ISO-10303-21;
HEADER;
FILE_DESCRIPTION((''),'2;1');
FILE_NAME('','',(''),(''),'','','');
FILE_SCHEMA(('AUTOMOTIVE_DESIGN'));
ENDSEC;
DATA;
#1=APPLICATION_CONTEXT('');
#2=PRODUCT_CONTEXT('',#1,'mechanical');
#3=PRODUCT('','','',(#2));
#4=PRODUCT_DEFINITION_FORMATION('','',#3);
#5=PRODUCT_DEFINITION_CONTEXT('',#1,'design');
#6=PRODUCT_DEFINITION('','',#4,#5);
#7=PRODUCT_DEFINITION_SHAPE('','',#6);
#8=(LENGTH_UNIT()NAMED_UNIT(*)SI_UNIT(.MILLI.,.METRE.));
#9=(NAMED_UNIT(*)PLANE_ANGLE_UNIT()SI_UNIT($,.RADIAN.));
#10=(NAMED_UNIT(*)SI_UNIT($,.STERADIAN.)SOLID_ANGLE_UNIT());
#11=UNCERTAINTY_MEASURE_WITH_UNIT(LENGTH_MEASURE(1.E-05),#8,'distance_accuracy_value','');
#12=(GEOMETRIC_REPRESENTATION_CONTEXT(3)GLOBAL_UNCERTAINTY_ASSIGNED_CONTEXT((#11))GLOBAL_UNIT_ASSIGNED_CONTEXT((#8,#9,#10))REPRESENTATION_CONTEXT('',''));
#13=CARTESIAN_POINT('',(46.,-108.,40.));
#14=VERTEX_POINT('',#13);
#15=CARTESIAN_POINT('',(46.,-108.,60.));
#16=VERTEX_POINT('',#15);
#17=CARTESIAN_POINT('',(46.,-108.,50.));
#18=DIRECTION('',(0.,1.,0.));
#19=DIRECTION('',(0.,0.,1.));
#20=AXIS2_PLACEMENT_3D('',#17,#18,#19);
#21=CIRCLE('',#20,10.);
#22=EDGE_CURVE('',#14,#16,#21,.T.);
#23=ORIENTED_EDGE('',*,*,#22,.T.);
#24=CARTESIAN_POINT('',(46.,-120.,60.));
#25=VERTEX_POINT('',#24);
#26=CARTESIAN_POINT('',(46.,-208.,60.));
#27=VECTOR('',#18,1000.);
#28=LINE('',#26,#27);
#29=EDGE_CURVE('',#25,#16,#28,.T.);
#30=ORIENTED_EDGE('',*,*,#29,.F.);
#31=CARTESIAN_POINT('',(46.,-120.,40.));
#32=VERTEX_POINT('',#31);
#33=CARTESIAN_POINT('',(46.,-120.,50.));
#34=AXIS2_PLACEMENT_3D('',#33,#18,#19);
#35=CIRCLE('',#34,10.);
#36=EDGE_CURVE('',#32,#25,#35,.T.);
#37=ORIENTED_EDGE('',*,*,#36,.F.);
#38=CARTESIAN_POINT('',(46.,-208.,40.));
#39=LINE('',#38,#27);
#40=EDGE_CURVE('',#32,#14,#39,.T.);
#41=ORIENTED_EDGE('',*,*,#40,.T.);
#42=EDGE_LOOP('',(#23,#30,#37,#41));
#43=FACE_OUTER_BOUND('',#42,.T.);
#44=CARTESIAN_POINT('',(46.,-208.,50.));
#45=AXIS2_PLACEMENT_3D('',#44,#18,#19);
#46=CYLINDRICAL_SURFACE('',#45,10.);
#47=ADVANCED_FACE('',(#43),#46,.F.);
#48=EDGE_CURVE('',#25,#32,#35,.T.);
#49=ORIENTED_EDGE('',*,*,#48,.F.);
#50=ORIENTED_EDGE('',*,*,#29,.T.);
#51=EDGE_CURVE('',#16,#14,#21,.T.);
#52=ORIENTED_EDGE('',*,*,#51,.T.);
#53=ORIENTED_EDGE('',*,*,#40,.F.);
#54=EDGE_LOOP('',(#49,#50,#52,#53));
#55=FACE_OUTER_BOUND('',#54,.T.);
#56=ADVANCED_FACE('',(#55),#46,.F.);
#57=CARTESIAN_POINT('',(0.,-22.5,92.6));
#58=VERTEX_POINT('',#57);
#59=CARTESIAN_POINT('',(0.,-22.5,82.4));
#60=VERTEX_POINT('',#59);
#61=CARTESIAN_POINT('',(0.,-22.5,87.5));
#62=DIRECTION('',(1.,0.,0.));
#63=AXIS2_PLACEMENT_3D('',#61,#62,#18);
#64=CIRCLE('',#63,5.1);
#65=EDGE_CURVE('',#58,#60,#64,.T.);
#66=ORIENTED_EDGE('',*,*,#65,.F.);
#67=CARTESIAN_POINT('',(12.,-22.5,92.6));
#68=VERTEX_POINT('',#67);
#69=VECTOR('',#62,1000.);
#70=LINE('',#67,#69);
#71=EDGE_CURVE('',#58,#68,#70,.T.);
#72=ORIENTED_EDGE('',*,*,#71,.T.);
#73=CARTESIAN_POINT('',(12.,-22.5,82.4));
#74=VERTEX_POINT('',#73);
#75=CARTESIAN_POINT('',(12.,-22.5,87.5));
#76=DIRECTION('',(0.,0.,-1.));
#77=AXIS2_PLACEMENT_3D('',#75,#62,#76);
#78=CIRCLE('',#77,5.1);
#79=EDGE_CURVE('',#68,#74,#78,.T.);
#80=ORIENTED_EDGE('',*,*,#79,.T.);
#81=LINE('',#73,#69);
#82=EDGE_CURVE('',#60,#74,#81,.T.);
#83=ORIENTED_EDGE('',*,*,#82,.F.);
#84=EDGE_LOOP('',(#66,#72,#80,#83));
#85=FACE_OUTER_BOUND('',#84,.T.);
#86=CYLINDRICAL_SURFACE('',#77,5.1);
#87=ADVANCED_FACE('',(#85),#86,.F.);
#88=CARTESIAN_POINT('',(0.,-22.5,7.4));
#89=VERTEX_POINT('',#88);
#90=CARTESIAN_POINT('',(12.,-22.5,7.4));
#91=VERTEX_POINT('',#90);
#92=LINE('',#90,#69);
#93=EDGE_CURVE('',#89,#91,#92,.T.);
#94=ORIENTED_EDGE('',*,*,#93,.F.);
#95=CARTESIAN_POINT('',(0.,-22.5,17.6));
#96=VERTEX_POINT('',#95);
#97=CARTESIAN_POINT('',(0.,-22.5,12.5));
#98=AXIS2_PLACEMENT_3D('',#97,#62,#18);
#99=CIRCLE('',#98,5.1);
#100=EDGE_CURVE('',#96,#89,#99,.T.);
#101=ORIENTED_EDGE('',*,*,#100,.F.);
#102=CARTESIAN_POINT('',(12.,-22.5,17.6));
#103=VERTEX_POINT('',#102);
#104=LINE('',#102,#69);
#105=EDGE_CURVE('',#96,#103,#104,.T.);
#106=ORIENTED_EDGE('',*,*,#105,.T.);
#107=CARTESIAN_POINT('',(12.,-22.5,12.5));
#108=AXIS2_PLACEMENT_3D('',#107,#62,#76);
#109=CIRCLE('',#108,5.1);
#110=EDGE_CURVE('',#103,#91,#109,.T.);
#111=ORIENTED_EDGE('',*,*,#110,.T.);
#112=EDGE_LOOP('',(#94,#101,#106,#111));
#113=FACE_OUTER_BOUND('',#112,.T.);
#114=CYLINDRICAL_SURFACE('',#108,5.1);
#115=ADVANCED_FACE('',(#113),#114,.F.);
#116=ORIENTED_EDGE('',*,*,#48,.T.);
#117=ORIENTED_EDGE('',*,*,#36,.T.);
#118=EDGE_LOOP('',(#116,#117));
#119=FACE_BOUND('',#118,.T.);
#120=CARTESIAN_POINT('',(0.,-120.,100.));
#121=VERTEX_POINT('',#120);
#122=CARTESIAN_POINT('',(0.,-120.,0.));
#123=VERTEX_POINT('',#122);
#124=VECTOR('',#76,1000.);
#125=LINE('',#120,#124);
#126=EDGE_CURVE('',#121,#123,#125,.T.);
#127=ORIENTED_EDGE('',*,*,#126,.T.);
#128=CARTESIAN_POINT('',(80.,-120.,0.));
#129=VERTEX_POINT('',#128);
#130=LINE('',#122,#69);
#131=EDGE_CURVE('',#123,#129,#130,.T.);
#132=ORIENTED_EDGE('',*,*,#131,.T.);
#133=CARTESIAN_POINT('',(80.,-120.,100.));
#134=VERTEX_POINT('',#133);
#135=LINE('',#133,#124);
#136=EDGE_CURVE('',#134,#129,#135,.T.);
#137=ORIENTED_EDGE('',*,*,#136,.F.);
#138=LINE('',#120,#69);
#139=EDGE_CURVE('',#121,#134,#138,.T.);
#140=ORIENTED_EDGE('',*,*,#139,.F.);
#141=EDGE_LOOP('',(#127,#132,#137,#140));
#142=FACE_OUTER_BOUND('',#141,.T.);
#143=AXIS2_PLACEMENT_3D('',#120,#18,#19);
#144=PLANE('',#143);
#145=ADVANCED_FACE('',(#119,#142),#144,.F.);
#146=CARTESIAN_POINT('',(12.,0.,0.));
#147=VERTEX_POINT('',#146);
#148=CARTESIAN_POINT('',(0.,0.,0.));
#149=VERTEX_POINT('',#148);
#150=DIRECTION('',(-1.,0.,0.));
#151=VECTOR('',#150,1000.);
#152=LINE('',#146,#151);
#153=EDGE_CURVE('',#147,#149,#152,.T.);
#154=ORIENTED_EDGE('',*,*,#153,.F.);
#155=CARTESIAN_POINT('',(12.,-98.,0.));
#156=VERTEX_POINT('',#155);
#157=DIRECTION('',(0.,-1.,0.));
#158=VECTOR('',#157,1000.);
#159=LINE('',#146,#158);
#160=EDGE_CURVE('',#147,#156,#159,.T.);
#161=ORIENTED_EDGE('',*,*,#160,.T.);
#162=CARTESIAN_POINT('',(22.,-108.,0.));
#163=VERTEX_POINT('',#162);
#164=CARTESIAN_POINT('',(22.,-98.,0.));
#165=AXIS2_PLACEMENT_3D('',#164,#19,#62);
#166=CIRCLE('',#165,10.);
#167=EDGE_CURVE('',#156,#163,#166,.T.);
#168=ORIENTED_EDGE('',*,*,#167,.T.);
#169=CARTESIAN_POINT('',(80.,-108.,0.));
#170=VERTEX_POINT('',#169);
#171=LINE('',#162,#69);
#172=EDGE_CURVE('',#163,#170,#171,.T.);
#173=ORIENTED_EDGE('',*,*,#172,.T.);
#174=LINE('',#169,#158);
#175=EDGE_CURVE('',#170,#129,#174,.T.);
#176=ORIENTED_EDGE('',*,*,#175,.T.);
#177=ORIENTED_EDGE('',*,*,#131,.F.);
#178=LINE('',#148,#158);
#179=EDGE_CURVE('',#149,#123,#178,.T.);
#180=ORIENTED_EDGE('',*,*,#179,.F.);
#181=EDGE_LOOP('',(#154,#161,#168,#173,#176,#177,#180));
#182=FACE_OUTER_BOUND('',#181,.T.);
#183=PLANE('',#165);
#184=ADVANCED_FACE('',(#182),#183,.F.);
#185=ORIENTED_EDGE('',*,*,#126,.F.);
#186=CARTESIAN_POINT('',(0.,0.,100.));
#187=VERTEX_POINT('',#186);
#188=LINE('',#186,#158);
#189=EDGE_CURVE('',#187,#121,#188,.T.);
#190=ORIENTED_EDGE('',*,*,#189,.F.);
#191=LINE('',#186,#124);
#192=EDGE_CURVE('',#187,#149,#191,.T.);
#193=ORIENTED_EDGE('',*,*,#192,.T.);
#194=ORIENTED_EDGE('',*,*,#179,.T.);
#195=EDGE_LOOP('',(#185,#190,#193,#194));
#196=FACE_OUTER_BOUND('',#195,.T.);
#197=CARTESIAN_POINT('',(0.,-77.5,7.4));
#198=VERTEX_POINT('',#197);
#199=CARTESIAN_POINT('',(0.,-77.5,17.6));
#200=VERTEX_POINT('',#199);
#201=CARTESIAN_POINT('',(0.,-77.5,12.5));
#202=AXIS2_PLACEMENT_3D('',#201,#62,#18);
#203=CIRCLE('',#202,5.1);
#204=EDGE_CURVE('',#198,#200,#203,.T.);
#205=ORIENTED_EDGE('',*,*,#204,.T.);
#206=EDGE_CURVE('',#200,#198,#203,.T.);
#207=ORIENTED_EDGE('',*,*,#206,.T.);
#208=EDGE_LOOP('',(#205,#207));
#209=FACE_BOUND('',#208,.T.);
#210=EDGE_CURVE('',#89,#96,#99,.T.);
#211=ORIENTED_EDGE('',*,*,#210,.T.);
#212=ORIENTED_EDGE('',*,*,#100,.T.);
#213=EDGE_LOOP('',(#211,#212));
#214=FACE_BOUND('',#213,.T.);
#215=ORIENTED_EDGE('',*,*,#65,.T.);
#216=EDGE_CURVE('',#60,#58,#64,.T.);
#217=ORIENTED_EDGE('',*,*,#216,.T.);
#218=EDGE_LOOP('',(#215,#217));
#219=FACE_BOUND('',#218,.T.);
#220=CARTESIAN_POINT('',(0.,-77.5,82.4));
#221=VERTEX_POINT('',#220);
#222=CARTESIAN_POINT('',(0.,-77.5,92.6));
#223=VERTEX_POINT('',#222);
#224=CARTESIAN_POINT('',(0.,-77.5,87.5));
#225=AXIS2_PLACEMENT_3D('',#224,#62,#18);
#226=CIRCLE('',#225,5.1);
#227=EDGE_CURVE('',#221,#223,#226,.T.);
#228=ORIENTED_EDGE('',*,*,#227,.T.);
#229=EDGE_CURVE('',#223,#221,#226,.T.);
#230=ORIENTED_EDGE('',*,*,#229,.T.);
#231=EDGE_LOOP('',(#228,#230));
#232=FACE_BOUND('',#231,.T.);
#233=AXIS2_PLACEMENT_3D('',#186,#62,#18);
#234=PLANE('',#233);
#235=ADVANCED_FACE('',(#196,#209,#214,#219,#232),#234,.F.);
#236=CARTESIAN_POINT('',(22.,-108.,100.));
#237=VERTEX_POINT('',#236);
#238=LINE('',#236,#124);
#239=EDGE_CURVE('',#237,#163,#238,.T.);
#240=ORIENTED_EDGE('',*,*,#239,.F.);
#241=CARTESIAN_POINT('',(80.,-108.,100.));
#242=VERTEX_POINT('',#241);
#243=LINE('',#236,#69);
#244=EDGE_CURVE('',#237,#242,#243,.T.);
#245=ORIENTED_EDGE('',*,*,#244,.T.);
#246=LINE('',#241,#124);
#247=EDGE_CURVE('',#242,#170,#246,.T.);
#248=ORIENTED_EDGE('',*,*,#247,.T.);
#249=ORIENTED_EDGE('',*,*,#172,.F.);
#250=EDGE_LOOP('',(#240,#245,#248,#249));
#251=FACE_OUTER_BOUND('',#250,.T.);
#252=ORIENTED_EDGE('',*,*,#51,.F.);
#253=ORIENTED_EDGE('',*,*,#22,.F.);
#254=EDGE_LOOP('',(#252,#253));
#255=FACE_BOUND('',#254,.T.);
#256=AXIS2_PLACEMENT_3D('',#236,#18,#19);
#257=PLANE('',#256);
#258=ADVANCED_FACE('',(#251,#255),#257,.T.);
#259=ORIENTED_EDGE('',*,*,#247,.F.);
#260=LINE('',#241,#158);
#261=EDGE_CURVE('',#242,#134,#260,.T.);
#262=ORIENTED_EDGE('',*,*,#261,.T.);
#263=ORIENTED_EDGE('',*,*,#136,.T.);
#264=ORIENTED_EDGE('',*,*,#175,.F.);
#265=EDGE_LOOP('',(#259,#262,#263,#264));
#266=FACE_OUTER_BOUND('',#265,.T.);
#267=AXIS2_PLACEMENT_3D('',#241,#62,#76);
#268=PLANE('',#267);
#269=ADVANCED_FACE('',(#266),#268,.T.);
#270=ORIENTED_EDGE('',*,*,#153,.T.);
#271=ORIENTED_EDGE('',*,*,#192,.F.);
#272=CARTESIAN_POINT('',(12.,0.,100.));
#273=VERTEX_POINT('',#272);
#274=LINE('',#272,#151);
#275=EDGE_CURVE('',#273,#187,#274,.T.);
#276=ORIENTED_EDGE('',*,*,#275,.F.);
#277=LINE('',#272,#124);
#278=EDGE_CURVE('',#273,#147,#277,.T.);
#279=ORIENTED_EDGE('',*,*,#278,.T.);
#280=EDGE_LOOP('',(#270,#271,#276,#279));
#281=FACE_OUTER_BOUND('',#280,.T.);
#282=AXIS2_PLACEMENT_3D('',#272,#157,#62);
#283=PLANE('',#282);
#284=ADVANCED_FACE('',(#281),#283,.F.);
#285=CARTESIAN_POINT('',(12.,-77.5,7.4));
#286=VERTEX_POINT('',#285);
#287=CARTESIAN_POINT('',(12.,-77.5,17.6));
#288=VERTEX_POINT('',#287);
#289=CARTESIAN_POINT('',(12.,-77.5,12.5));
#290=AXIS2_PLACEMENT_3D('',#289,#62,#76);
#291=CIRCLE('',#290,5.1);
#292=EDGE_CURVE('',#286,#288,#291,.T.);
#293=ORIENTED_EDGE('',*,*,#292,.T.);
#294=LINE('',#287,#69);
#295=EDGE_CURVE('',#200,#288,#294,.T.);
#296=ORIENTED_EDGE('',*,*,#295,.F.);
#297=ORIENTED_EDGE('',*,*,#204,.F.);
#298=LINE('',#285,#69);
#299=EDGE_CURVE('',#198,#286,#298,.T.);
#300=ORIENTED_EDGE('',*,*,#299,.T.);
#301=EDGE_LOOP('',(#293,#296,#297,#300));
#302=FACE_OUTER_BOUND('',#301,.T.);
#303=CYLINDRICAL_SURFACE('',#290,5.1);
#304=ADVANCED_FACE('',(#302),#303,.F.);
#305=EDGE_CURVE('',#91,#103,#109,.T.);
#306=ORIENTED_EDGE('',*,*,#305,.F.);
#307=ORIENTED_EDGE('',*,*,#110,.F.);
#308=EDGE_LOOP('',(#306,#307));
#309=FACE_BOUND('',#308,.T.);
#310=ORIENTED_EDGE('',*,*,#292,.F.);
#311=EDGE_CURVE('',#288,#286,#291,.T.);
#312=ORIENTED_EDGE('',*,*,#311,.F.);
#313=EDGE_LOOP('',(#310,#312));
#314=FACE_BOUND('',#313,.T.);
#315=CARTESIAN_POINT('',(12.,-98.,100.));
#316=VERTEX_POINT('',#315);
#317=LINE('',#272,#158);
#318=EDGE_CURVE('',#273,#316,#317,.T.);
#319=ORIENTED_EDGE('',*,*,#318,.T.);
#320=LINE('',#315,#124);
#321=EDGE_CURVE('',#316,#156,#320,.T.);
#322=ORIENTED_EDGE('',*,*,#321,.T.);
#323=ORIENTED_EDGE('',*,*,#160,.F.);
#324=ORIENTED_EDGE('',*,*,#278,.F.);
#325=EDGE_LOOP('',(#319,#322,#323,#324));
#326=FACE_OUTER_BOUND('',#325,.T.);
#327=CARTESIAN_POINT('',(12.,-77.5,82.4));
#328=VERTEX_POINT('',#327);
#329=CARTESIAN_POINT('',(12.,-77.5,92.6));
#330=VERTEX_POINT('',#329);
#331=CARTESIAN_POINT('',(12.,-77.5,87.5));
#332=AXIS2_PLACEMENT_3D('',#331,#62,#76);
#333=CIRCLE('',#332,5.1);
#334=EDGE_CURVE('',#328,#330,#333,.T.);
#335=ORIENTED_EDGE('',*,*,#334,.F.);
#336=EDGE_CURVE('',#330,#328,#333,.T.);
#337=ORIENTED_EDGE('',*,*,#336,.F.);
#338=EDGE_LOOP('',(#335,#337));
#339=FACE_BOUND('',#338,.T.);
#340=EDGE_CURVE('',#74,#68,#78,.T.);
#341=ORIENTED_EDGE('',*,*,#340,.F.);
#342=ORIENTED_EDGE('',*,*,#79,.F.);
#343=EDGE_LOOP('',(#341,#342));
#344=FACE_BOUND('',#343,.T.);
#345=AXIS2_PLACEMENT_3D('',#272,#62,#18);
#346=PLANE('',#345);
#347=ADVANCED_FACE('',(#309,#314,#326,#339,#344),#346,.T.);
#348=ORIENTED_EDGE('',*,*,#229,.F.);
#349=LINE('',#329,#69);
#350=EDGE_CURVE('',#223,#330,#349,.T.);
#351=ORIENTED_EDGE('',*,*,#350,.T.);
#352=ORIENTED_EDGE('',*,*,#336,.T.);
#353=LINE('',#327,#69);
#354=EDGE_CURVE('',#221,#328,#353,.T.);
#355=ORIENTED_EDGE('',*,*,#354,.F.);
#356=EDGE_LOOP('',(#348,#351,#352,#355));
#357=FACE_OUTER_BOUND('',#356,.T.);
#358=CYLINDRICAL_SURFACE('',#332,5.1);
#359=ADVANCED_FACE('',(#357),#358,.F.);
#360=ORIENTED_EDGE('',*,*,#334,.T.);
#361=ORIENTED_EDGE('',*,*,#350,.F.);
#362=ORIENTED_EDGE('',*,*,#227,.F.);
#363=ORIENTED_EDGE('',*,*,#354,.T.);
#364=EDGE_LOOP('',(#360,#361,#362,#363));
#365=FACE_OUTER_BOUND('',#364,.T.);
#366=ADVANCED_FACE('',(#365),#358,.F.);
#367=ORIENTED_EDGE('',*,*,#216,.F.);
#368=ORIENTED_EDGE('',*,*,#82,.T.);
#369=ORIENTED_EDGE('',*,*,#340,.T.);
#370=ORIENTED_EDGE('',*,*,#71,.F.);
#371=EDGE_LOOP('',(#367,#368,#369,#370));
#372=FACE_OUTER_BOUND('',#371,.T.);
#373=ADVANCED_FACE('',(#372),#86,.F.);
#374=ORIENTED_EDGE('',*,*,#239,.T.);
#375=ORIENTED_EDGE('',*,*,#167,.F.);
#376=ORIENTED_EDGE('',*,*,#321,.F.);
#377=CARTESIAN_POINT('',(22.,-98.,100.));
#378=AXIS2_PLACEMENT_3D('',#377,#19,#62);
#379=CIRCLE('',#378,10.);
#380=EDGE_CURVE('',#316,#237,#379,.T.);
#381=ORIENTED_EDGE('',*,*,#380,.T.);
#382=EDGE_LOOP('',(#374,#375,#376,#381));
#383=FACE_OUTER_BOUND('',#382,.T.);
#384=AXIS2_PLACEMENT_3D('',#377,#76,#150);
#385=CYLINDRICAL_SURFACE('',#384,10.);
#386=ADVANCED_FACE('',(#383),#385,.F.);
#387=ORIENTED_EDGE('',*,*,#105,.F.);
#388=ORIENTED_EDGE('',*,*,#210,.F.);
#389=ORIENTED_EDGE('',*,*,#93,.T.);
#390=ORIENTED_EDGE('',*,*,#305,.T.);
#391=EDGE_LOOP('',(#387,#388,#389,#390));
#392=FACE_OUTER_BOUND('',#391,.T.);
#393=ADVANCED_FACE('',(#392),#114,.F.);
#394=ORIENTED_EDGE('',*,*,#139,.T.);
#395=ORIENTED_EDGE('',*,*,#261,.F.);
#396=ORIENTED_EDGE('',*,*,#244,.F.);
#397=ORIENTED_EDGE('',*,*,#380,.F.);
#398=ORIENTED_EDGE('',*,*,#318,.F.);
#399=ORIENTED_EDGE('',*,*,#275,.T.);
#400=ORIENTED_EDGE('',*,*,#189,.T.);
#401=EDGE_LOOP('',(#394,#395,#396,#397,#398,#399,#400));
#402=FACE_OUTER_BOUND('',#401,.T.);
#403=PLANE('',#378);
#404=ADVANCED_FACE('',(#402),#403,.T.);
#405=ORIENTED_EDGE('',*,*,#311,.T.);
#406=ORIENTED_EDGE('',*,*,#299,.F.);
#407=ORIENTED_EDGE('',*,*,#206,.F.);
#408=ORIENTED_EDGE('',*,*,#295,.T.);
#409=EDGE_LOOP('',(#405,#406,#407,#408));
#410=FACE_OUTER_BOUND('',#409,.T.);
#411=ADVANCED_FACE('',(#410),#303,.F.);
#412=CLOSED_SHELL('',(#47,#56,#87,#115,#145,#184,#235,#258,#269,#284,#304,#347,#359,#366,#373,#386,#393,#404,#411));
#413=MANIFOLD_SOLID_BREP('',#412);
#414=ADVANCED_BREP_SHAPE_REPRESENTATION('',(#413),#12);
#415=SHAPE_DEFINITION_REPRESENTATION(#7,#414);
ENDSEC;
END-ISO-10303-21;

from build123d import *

# Parameters (mm, degrees)
BOSS_EXTRUDE1_DEPTH    = 100
M12_TAPPED_HOLE1_D     = 10.2
M12_TAPPED_HOLE1_DEPTH = 29.25
M12_TAPPED_HOLE1_TIP   = 3.064389157
SKETCH5_R              = 10
CUT_EXTRUDE1_DEPTH     = 100


with BuildPart() as part:
    # Sketch1 → Boss-Extrude1 (new body)
    with BuildSketch(Plane.XY):
        with BuildLine():
            Line((0, 0), (0, -120))
            Line((0, -120), (80, -120))
            Line((80, -120), (80, -108))
            Line((80, -108), (22, -108))
            ThreePointArc((22, -108), (14.928932188, -105.071067812), (12, -98))
            Line((12, -98), (12, 0))
            Line((12, 0), (0, 0))
        make_face()
    extrude(amount=BOSS_EXTRUDE1_DEPTH)

    # M12 Tapped Hole1
    with Locations(Plane(origin=(12, 0, 0), x_dir=(0, 0, -1), z_dir=(1, 0, 0))):
        with Locations((-87.5, -22.5), (-12.5, -22.5), (-12.5, -77.5), (-87.5, -77.5)):
            Hole(M12_TAPPED_HOLE1_D / 2, depth=M12_TAPPED_HOLE1_DEPTH)
            with Locations((0, 0, -(M12_TAPPED_HOLE1_DEPTH + M12_TAPPED_HOLE1_TIP / 2))):  # 118° drill point
                Cone(0, M12_TAPPED_HOLE1_D / 2, M12_TAPPED_HOLE1_TIP, mode=Mode.SUBTRACT)

    # Sketch5 → Cut-Extrude1 (cut)
    with BuildSketch(Plane(origin=(0, -108, 0), x_dir=(1, 0, 0), z_dir=(0, 1, 0))):
        with Locations(Location((46, -50, 0), (0, 0, 270))):
            Circle(SKETCH5_R)
    extrude(amount=-CUT_EXTRUDE1_DEPTH, mode=Mode.SUBTRACT)


solid = part.part
